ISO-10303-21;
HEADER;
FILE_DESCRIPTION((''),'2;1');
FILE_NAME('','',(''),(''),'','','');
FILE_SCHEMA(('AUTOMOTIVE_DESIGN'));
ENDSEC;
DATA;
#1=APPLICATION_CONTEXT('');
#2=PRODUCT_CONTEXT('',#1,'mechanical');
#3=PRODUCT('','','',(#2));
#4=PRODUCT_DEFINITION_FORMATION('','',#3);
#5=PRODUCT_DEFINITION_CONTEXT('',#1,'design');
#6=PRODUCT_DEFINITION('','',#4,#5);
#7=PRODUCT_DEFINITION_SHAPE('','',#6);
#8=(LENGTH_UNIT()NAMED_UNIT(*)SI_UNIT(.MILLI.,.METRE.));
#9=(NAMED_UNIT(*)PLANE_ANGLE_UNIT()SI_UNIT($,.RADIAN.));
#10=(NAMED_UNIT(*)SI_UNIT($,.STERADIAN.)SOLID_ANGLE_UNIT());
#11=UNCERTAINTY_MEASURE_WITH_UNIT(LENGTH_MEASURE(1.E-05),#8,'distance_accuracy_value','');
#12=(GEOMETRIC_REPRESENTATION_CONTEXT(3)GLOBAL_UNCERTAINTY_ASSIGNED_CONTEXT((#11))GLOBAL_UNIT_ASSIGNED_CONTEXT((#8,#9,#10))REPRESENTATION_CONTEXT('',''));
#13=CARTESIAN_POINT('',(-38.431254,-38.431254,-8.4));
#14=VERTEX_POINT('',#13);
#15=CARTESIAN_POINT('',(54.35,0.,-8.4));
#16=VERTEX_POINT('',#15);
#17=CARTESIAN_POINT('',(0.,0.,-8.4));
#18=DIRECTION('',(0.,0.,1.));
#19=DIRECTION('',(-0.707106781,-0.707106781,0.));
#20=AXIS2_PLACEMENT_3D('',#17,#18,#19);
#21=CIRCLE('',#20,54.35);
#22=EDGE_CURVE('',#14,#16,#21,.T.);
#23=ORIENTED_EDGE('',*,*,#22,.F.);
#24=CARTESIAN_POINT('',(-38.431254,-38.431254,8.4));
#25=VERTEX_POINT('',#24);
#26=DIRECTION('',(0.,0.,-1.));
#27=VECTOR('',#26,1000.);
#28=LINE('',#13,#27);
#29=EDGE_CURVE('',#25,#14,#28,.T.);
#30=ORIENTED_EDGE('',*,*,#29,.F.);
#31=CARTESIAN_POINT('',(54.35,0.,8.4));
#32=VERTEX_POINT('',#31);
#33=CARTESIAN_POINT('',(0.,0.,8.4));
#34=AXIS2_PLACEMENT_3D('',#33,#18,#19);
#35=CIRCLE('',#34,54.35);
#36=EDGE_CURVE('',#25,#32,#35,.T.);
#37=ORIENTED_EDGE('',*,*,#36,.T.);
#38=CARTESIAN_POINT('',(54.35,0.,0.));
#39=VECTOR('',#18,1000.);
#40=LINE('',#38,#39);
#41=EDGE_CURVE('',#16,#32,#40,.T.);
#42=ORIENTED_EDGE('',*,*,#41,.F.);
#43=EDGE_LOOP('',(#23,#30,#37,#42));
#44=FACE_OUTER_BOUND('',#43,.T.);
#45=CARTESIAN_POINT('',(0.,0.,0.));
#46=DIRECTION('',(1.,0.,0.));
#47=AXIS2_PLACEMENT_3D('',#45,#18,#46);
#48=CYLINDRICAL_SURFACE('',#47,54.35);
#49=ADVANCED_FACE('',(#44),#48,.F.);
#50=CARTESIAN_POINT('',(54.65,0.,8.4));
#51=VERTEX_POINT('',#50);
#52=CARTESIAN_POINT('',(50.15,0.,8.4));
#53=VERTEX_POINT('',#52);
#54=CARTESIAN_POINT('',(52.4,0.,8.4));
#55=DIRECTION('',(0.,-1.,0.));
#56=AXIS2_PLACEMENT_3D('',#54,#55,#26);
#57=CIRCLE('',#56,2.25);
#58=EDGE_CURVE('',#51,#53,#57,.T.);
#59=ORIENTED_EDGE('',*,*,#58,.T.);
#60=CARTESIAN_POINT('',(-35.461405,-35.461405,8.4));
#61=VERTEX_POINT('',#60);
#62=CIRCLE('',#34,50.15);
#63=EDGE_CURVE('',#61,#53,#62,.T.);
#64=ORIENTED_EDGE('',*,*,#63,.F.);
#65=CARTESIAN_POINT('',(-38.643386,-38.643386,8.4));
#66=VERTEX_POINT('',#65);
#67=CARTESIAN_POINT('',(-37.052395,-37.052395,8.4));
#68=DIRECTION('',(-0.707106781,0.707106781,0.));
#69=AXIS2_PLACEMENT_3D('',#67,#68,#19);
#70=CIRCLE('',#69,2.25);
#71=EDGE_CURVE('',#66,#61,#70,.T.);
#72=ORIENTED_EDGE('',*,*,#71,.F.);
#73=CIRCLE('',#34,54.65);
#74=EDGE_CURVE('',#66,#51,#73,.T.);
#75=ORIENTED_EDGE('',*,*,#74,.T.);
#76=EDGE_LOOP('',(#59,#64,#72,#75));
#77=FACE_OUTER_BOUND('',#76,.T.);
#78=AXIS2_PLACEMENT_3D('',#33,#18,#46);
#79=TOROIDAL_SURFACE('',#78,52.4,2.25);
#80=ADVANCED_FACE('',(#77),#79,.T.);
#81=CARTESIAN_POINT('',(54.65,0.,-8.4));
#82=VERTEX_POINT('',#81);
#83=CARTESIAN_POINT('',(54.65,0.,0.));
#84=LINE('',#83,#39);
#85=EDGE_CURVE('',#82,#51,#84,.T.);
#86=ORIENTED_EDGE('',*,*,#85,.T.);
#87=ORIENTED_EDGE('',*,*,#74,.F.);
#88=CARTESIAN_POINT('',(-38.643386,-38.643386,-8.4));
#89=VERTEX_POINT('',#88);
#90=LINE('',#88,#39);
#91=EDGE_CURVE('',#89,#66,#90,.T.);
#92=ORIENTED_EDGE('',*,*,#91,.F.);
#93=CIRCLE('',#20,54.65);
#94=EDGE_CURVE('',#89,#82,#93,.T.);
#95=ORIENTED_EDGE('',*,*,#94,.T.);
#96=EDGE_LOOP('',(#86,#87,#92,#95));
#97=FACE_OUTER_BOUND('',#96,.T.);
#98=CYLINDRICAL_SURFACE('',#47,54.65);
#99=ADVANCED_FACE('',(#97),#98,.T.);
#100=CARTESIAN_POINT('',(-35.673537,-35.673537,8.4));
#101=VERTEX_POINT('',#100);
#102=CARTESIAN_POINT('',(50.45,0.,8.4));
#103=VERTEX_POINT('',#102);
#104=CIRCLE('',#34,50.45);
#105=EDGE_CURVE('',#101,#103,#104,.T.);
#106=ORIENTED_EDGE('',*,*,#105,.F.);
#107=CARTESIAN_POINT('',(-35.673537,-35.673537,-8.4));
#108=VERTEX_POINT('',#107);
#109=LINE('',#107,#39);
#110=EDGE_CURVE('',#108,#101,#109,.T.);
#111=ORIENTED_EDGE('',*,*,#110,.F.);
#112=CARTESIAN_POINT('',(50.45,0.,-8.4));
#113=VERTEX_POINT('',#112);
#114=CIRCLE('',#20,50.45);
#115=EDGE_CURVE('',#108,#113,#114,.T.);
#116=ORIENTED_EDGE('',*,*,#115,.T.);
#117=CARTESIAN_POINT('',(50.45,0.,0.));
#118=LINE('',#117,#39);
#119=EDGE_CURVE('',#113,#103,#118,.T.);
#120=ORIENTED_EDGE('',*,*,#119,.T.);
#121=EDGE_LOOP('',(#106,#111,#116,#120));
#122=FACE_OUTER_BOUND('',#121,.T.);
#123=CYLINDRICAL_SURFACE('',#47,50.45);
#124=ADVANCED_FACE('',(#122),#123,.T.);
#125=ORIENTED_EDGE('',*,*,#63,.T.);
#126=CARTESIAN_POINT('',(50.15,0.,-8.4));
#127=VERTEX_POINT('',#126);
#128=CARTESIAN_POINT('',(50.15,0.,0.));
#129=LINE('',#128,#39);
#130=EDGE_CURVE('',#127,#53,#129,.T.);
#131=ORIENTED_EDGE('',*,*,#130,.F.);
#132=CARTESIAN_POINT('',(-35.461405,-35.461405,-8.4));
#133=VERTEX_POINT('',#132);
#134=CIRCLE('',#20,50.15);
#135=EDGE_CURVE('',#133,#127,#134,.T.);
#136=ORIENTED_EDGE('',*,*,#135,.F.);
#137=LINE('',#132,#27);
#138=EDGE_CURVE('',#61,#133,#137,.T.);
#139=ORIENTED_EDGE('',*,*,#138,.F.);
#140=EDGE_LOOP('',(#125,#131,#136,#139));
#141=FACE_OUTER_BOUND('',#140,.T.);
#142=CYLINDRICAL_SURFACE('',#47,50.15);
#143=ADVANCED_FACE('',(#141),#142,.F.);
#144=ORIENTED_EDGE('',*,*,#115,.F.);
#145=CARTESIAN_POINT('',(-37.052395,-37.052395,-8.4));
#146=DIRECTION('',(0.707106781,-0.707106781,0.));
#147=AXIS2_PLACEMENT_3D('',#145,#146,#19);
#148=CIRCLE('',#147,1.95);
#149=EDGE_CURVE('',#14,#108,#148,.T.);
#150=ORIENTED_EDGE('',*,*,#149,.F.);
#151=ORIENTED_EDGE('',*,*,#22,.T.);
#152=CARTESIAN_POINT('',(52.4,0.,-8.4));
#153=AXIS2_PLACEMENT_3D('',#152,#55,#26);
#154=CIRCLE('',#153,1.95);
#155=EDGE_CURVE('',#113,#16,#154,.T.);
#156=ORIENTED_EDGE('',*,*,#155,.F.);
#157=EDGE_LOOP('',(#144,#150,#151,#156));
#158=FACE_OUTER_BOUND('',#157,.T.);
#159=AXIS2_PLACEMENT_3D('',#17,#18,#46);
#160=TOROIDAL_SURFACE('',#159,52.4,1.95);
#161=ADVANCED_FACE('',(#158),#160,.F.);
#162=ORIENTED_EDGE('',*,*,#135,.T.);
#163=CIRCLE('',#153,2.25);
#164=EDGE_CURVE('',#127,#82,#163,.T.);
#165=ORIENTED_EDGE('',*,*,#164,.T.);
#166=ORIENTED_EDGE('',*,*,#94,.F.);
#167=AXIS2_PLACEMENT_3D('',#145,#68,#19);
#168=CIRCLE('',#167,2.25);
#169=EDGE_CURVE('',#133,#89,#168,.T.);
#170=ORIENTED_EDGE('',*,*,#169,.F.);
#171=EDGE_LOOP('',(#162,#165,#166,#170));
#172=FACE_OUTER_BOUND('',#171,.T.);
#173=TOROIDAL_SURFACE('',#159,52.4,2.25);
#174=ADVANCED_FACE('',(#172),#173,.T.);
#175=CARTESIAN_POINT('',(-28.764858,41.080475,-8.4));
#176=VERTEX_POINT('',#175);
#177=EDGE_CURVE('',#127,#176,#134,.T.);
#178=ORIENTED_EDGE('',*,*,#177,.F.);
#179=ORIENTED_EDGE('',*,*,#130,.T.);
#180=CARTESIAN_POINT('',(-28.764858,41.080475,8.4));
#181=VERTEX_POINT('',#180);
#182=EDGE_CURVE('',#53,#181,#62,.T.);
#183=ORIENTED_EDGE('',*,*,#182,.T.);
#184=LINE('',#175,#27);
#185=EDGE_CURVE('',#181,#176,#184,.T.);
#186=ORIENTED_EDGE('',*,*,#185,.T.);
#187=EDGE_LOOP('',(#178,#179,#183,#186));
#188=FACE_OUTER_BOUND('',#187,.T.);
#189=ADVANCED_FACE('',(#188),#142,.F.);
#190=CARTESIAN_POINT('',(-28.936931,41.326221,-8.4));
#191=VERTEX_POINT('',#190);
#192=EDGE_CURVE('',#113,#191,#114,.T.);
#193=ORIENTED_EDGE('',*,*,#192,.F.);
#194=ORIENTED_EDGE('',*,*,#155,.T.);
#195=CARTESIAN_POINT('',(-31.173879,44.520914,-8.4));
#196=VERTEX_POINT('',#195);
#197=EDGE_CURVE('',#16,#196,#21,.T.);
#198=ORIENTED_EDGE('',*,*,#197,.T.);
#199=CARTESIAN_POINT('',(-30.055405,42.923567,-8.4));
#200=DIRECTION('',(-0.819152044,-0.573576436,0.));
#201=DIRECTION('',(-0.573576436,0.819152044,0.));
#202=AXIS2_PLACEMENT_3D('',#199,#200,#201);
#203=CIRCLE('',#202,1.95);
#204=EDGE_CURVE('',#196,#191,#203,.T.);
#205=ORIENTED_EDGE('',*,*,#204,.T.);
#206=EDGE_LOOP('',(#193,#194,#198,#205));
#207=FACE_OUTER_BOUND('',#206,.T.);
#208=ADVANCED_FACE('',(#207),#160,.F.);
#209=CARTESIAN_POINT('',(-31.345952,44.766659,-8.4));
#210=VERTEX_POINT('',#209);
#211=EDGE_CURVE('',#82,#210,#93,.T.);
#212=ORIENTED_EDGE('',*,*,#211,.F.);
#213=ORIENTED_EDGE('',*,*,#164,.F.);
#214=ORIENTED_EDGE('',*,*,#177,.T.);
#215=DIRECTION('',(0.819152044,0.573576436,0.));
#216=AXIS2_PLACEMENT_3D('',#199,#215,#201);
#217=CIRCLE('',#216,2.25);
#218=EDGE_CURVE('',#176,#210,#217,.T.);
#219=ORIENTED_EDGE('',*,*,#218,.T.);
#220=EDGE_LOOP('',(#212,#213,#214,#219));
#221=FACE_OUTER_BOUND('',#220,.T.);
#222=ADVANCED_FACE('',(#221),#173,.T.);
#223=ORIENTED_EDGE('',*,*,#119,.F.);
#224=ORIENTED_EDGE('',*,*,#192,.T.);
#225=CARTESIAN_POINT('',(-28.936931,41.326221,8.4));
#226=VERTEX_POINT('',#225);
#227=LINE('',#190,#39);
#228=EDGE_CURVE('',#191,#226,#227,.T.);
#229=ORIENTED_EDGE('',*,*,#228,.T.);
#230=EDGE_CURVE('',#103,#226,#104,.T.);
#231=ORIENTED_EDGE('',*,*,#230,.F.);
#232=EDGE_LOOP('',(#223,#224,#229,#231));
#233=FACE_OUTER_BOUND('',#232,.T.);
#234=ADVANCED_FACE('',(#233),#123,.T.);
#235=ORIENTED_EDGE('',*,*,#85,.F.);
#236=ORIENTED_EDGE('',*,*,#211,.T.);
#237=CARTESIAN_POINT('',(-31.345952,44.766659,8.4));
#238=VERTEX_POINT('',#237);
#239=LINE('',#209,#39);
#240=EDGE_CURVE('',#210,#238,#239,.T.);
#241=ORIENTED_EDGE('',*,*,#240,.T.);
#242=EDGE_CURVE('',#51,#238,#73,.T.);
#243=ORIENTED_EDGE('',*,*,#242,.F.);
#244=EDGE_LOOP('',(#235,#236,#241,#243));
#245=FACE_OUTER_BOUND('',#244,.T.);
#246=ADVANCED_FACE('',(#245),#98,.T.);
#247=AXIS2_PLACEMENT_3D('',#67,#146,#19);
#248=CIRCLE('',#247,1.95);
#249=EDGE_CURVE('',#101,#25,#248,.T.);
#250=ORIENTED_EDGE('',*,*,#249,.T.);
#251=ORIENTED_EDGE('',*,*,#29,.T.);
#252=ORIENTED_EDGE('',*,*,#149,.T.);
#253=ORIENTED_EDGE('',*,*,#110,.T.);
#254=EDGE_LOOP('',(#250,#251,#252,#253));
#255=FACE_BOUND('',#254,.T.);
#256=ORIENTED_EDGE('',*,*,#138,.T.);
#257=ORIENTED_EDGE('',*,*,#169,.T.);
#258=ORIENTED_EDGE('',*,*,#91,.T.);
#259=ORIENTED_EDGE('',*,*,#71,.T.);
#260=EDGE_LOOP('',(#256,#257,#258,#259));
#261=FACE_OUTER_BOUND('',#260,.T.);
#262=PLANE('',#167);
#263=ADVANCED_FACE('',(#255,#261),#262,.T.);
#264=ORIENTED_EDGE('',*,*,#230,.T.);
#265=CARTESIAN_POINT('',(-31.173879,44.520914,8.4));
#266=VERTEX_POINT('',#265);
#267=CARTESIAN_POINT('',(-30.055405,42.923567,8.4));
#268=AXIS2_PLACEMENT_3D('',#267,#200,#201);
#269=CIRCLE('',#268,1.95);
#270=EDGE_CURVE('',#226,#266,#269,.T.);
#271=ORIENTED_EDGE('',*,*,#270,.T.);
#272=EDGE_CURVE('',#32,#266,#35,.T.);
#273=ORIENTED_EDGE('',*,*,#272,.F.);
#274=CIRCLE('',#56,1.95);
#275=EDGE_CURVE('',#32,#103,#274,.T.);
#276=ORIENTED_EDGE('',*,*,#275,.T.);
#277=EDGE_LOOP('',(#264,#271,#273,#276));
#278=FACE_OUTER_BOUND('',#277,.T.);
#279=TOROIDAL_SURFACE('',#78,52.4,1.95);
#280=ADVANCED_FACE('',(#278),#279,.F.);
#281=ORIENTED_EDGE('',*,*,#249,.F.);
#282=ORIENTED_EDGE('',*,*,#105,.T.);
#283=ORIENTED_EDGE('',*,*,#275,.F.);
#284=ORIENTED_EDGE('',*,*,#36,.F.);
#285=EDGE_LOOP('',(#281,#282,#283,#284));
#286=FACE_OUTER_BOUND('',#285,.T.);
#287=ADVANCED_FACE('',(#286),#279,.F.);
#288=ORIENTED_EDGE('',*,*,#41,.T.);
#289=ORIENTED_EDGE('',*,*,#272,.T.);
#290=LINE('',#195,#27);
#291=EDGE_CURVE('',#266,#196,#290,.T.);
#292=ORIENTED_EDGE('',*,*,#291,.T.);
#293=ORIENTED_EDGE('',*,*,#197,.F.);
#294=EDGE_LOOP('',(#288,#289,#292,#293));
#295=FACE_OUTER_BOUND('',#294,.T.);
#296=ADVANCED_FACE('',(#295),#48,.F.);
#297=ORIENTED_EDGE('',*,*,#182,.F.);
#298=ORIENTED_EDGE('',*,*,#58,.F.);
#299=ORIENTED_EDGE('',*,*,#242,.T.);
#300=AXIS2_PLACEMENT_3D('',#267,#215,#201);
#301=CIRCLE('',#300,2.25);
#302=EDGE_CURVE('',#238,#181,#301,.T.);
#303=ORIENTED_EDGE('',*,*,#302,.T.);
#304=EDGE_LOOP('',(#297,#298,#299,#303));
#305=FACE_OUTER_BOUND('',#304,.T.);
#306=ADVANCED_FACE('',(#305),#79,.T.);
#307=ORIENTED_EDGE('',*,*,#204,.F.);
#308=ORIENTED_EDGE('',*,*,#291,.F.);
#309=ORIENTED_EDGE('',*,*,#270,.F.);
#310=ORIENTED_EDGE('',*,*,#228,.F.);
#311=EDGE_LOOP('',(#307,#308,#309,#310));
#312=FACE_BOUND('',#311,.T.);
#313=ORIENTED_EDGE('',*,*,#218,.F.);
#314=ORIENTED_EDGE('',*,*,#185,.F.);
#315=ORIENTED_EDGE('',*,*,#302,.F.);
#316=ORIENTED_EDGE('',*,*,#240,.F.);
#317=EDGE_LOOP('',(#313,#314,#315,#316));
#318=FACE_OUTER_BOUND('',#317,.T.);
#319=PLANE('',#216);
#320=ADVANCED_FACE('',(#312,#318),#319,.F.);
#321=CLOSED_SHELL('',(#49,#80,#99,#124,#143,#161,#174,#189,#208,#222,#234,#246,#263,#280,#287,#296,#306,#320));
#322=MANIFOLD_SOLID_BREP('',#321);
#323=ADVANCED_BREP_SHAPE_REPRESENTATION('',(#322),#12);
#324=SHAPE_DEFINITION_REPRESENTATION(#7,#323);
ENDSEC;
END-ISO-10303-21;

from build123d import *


with BuildPart() as part:
    # Sweep 2: sweep along a path in Sketch 1
    with BuildLine(Plane.XY) as sweep_2_path:
        ThreePointArc((-37.052395334, -37.052395334), (52.20060218, -4.56696092), (-30.055405265, 42.923567121))
    # Sketch 2 → Sweep 2 (sweep)
    with BuildSketch(Plane(origin=(0, 0, 0), x_dir=(-0.5735764363510427, 0.8191520442889942, 0), z_dir=(0.8191520442889942, 0.5735764363510427, 0))):
        with BuildLine():
            Line((50.15, -8.4), (50.15, 8.4))
            ThreePointArc((50.15, 8.4), (52.4, 10.65), (54.65, 8.4))
            Line((54.65, 8.4), (54.65, -8.4))
            ThreePointArc((54.65, -8.4), (52.4, -10.65), (50.15, -8.4))
        make_face()
        with BuildLine():
            Line((50.45, -8.4), (50.45, 8.4))
            ThreePointArc((50.45, 8.4), (52.4, 10.35), (54.35, 8.4))
            Line((54.35, 8.4), (54.35, -8.4))
            ThreePointArc((54.35, -8.4), (52.4, -10.35), (50.45, -8.4))
        make_face(mode=Mode.SUBTRACT)
    sweep(path=sweep_2_path.line)


solid = part.part
